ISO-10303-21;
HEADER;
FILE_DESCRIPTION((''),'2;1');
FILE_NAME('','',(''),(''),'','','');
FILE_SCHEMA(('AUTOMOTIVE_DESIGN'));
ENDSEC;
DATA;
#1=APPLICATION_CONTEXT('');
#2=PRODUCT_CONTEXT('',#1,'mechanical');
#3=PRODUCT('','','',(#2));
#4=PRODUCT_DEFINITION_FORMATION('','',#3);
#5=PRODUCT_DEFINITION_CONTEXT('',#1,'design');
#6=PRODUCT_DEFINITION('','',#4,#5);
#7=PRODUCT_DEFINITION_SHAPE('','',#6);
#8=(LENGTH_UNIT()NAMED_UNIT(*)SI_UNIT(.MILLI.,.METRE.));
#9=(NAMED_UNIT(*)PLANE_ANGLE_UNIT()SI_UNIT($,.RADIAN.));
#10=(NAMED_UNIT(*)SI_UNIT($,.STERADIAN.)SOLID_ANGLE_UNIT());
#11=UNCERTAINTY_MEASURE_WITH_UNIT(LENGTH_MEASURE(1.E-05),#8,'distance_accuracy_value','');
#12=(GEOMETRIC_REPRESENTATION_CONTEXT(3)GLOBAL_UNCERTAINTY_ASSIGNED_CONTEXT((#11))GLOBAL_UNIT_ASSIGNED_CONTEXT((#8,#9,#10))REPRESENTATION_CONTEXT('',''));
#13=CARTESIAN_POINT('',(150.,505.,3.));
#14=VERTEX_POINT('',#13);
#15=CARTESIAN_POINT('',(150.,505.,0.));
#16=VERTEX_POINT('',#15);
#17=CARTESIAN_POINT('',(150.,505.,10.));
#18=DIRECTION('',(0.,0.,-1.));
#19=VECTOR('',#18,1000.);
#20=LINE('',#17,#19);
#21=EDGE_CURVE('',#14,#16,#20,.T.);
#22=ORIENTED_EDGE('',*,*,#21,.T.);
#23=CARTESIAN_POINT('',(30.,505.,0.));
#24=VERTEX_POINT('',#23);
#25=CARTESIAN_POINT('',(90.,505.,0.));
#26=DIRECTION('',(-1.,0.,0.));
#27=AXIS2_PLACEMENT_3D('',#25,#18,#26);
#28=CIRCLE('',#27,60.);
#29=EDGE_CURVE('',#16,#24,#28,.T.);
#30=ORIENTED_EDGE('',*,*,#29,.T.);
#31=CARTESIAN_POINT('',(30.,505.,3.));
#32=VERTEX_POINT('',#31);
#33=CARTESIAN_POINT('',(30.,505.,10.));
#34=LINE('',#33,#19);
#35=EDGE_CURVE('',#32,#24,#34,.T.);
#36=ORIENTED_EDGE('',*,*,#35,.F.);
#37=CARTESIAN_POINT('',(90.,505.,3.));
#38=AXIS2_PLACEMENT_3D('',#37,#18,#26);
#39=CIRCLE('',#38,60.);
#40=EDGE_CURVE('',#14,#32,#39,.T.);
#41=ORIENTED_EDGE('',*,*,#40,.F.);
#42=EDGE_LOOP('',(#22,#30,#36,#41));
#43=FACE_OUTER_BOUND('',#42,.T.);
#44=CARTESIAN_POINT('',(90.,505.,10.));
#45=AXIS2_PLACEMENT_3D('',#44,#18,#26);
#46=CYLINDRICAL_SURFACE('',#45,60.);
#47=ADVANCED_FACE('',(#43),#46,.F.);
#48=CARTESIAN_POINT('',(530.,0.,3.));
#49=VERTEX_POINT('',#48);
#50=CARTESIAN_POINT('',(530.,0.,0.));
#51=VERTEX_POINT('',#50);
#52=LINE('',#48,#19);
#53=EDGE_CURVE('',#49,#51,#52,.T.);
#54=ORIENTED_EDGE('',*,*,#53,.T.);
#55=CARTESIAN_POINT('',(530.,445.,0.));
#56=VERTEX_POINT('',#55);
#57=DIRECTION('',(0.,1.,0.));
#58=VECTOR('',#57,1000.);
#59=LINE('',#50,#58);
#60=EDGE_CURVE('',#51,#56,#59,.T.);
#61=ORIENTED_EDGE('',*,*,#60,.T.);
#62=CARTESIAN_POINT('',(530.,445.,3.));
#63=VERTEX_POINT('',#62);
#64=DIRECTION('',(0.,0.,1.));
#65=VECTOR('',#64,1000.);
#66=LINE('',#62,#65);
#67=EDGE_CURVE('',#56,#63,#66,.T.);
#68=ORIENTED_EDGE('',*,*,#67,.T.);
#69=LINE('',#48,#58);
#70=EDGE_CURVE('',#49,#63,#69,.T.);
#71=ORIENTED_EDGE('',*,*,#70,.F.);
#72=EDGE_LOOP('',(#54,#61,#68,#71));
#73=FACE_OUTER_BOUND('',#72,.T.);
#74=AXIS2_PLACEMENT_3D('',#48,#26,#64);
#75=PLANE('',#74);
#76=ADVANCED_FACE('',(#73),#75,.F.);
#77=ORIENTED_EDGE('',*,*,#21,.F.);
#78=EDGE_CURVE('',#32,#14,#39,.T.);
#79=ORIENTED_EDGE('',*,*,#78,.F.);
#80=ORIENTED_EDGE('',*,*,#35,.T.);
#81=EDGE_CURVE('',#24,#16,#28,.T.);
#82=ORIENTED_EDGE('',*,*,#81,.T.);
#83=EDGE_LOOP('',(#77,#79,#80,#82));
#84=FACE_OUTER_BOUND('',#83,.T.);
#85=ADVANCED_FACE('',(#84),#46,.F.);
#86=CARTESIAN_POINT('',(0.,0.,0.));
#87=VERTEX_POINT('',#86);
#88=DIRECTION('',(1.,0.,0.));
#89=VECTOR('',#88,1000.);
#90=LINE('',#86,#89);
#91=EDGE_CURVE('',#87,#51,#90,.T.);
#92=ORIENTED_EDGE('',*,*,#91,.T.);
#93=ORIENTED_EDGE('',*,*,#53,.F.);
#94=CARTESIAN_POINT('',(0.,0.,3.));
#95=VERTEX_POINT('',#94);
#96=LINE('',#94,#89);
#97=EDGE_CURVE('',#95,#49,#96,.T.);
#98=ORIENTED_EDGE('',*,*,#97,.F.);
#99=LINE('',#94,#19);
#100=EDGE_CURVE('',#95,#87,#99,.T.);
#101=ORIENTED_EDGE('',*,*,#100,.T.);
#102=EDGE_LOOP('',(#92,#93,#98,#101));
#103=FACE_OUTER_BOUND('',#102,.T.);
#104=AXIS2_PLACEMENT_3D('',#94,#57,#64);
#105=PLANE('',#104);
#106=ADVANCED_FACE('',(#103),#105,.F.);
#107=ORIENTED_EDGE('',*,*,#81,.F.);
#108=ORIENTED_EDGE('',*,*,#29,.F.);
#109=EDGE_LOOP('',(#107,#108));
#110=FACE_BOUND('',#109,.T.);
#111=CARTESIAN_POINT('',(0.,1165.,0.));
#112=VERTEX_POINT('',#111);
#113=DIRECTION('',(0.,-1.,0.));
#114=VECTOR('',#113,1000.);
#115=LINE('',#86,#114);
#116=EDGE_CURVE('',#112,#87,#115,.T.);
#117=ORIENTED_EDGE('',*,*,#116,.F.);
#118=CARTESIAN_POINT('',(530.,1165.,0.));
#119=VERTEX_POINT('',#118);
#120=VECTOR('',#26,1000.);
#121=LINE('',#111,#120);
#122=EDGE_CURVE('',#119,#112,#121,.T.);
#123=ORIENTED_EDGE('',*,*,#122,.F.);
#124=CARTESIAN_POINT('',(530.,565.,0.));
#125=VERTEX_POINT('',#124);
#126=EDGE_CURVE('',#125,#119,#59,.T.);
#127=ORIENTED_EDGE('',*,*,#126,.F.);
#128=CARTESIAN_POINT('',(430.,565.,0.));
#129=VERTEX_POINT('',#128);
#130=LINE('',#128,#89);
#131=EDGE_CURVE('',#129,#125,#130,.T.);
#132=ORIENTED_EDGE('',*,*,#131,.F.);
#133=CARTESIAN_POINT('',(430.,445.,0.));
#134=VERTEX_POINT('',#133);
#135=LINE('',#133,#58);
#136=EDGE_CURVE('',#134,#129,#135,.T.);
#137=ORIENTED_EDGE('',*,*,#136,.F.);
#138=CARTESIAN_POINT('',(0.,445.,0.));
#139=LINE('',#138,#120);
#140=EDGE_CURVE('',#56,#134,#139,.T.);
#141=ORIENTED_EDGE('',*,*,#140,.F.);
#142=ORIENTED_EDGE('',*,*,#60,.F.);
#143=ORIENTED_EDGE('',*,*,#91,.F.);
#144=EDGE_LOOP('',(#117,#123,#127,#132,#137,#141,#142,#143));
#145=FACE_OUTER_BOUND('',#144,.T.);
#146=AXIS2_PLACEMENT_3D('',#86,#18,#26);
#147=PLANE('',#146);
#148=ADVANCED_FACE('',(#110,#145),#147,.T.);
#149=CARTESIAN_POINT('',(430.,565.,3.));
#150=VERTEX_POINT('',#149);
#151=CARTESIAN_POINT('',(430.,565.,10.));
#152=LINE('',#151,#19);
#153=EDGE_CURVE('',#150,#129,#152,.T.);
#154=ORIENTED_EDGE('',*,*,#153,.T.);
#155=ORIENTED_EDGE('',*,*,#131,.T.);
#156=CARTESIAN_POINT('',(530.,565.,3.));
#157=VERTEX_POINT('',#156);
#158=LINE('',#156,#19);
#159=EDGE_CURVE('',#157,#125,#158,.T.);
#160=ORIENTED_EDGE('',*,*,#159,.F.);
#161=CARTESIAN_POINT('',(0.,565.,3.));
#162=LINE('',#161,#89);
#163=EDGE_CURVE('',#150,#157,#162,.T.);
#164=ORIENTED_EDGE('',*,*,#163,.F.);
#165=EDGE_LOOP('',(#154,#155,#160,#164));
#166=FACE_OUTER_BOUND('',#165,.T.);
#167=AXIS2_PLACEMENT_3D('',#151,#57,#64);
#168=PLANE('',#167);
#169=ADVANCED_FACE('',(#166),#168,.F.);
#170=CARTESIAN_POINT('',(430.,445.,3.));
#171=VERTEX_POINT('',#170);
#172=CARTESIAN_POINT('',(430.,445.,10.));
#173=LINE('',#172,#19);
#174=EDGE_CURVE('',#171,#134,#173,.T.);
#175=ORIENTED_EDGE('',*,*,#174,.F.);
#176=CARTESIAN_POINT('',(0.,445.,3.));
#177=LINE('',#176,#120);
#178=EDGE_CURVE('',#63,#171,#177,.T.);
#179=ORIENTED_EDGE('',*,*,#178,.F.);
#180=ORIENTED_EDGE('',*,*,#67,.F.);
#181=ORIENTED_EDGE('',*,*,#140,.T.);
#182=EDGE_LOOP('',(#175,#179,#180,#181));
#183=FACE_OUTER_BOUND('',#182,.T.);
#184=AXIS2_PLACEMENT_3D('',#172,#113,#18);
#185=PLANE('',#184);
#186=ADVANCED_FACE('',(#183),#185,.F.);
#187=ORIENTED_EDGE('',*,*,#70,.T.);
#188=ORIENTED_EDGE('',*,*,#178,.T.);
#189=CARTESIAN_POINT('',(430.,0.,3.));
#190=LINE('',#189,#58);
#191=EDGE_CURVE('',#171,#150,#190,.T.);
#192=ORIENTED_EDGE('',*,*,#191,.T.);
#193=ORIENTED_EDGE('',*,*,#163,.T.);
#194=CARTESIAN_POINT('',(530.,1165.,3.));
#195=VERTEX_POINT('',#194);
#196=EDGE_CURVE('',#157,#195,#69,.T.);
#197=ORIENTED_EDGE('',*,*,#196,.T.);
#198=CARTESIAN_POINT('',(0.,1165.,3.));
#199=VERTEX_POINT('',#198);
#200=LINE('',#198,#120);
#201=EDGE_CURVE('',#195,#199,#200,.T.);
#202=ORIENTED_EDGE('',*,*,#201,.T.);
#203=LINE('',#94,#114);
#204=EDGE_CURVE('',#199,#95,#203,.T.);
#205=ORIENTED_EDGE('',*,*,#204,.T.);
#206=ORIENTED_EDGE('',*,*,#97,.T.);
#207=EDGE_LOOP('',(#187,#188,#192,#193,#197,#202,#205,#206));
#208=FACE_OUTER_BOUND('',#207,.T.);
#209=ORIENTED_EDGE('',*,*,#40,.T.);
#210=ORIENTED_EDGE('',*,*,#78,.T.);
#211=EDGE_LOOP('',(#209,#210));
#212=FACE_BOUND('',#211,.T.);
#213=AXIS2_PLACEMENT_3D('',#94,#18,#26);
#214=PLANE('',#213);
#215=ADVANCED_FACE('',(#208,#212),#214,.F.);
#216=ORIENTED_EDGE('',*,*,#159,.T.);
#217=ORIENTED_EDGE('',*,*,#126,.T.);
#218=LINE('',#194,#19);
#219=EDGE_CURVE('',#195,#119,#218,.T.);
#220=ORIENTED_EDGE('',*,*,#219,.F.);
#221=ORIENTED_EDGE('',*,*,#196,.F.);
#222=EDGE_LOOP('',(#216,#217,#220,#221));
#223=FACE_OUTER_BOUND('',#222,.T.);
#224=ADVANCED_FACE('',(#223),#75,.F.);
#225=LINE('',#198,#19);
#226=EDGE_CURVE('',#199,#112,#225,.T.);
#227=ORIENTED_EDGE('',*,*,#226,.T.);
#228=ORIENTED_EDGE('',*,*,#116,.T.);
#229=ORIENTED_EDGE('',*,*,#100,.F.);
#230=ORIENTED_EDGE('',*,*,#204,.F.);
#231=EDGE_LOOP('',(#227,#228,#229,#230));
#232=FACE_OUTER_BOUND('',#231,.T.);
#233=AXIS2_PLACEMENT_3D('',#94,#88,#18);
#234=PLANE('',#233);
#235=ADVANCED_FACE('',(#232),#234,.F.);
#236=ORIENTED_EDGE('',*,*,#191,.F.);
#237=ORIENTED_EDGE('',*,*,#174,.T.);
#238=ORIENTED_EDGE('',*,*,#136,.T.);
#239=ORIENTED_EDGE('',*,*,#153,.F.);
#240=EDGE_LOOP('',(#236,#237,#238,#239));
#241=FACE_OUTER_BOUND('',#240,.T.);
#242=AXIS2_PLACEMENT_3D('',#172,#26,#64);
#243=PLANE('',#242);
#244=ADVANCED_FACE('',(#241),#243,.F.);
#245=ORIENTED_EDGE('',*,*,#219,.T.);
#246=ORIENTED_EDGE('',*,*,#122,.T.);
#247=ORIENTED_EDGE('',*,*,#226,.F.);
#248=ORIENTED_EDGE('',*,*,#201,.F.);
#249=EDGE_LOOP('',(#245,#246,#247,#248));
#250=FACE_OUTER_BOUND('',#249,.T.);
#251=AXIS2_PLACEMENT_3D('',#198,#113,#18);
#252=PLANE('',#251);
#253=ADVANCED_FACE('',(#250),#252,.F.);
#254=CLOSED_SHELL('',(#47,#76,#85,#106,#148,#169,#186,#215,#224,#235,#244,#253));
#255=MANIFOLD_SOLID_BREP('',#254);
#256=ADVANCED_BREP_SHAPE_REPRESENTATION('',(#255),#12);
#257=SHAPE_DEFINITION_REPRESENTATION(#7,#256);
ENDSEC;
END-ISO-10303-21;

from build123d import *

# Parameters (mm, degrees)
SKETCH1_W           = 530
SKETCH1_H           = 1165
BOSS_EXTRUDE1_DEPTH = 3
SKETCH2_R           = 60
SKETCH2_W           = 120
SKETCH2_H           = 120
CUT_EXTRUDE1_DEPTH  = 10


with BuildPart() as part:
    # Sketch1 → Boss-Extrude1 (new body)
    with BuildSketch(Plane.XY):
        with Locations((265, 582.5)):
            Rectangle(SKETCH1_W, SKETCH1_H)
    extrude(amount=BOSS_EXTRUDE1_DEPTH)

    # Sketch2 → Cut-Extrude1 (cut)
    with BuildSketch(Plane(origin=(0, 0, 0), x_dir=(-1, 0, 0), z_dir=(0, 0, -1))):
        with Locations((-90, 505)):
            Circle(SKETCH2_R)
        with Locations((-490, 505)):
            Rectangle(SKETCH2_W, SKETCH2_H)
    extrude(amount=-CUT_EXTRUDE1_DEPTH, mode=Mode.SUBTRACT)


solid = part.part
